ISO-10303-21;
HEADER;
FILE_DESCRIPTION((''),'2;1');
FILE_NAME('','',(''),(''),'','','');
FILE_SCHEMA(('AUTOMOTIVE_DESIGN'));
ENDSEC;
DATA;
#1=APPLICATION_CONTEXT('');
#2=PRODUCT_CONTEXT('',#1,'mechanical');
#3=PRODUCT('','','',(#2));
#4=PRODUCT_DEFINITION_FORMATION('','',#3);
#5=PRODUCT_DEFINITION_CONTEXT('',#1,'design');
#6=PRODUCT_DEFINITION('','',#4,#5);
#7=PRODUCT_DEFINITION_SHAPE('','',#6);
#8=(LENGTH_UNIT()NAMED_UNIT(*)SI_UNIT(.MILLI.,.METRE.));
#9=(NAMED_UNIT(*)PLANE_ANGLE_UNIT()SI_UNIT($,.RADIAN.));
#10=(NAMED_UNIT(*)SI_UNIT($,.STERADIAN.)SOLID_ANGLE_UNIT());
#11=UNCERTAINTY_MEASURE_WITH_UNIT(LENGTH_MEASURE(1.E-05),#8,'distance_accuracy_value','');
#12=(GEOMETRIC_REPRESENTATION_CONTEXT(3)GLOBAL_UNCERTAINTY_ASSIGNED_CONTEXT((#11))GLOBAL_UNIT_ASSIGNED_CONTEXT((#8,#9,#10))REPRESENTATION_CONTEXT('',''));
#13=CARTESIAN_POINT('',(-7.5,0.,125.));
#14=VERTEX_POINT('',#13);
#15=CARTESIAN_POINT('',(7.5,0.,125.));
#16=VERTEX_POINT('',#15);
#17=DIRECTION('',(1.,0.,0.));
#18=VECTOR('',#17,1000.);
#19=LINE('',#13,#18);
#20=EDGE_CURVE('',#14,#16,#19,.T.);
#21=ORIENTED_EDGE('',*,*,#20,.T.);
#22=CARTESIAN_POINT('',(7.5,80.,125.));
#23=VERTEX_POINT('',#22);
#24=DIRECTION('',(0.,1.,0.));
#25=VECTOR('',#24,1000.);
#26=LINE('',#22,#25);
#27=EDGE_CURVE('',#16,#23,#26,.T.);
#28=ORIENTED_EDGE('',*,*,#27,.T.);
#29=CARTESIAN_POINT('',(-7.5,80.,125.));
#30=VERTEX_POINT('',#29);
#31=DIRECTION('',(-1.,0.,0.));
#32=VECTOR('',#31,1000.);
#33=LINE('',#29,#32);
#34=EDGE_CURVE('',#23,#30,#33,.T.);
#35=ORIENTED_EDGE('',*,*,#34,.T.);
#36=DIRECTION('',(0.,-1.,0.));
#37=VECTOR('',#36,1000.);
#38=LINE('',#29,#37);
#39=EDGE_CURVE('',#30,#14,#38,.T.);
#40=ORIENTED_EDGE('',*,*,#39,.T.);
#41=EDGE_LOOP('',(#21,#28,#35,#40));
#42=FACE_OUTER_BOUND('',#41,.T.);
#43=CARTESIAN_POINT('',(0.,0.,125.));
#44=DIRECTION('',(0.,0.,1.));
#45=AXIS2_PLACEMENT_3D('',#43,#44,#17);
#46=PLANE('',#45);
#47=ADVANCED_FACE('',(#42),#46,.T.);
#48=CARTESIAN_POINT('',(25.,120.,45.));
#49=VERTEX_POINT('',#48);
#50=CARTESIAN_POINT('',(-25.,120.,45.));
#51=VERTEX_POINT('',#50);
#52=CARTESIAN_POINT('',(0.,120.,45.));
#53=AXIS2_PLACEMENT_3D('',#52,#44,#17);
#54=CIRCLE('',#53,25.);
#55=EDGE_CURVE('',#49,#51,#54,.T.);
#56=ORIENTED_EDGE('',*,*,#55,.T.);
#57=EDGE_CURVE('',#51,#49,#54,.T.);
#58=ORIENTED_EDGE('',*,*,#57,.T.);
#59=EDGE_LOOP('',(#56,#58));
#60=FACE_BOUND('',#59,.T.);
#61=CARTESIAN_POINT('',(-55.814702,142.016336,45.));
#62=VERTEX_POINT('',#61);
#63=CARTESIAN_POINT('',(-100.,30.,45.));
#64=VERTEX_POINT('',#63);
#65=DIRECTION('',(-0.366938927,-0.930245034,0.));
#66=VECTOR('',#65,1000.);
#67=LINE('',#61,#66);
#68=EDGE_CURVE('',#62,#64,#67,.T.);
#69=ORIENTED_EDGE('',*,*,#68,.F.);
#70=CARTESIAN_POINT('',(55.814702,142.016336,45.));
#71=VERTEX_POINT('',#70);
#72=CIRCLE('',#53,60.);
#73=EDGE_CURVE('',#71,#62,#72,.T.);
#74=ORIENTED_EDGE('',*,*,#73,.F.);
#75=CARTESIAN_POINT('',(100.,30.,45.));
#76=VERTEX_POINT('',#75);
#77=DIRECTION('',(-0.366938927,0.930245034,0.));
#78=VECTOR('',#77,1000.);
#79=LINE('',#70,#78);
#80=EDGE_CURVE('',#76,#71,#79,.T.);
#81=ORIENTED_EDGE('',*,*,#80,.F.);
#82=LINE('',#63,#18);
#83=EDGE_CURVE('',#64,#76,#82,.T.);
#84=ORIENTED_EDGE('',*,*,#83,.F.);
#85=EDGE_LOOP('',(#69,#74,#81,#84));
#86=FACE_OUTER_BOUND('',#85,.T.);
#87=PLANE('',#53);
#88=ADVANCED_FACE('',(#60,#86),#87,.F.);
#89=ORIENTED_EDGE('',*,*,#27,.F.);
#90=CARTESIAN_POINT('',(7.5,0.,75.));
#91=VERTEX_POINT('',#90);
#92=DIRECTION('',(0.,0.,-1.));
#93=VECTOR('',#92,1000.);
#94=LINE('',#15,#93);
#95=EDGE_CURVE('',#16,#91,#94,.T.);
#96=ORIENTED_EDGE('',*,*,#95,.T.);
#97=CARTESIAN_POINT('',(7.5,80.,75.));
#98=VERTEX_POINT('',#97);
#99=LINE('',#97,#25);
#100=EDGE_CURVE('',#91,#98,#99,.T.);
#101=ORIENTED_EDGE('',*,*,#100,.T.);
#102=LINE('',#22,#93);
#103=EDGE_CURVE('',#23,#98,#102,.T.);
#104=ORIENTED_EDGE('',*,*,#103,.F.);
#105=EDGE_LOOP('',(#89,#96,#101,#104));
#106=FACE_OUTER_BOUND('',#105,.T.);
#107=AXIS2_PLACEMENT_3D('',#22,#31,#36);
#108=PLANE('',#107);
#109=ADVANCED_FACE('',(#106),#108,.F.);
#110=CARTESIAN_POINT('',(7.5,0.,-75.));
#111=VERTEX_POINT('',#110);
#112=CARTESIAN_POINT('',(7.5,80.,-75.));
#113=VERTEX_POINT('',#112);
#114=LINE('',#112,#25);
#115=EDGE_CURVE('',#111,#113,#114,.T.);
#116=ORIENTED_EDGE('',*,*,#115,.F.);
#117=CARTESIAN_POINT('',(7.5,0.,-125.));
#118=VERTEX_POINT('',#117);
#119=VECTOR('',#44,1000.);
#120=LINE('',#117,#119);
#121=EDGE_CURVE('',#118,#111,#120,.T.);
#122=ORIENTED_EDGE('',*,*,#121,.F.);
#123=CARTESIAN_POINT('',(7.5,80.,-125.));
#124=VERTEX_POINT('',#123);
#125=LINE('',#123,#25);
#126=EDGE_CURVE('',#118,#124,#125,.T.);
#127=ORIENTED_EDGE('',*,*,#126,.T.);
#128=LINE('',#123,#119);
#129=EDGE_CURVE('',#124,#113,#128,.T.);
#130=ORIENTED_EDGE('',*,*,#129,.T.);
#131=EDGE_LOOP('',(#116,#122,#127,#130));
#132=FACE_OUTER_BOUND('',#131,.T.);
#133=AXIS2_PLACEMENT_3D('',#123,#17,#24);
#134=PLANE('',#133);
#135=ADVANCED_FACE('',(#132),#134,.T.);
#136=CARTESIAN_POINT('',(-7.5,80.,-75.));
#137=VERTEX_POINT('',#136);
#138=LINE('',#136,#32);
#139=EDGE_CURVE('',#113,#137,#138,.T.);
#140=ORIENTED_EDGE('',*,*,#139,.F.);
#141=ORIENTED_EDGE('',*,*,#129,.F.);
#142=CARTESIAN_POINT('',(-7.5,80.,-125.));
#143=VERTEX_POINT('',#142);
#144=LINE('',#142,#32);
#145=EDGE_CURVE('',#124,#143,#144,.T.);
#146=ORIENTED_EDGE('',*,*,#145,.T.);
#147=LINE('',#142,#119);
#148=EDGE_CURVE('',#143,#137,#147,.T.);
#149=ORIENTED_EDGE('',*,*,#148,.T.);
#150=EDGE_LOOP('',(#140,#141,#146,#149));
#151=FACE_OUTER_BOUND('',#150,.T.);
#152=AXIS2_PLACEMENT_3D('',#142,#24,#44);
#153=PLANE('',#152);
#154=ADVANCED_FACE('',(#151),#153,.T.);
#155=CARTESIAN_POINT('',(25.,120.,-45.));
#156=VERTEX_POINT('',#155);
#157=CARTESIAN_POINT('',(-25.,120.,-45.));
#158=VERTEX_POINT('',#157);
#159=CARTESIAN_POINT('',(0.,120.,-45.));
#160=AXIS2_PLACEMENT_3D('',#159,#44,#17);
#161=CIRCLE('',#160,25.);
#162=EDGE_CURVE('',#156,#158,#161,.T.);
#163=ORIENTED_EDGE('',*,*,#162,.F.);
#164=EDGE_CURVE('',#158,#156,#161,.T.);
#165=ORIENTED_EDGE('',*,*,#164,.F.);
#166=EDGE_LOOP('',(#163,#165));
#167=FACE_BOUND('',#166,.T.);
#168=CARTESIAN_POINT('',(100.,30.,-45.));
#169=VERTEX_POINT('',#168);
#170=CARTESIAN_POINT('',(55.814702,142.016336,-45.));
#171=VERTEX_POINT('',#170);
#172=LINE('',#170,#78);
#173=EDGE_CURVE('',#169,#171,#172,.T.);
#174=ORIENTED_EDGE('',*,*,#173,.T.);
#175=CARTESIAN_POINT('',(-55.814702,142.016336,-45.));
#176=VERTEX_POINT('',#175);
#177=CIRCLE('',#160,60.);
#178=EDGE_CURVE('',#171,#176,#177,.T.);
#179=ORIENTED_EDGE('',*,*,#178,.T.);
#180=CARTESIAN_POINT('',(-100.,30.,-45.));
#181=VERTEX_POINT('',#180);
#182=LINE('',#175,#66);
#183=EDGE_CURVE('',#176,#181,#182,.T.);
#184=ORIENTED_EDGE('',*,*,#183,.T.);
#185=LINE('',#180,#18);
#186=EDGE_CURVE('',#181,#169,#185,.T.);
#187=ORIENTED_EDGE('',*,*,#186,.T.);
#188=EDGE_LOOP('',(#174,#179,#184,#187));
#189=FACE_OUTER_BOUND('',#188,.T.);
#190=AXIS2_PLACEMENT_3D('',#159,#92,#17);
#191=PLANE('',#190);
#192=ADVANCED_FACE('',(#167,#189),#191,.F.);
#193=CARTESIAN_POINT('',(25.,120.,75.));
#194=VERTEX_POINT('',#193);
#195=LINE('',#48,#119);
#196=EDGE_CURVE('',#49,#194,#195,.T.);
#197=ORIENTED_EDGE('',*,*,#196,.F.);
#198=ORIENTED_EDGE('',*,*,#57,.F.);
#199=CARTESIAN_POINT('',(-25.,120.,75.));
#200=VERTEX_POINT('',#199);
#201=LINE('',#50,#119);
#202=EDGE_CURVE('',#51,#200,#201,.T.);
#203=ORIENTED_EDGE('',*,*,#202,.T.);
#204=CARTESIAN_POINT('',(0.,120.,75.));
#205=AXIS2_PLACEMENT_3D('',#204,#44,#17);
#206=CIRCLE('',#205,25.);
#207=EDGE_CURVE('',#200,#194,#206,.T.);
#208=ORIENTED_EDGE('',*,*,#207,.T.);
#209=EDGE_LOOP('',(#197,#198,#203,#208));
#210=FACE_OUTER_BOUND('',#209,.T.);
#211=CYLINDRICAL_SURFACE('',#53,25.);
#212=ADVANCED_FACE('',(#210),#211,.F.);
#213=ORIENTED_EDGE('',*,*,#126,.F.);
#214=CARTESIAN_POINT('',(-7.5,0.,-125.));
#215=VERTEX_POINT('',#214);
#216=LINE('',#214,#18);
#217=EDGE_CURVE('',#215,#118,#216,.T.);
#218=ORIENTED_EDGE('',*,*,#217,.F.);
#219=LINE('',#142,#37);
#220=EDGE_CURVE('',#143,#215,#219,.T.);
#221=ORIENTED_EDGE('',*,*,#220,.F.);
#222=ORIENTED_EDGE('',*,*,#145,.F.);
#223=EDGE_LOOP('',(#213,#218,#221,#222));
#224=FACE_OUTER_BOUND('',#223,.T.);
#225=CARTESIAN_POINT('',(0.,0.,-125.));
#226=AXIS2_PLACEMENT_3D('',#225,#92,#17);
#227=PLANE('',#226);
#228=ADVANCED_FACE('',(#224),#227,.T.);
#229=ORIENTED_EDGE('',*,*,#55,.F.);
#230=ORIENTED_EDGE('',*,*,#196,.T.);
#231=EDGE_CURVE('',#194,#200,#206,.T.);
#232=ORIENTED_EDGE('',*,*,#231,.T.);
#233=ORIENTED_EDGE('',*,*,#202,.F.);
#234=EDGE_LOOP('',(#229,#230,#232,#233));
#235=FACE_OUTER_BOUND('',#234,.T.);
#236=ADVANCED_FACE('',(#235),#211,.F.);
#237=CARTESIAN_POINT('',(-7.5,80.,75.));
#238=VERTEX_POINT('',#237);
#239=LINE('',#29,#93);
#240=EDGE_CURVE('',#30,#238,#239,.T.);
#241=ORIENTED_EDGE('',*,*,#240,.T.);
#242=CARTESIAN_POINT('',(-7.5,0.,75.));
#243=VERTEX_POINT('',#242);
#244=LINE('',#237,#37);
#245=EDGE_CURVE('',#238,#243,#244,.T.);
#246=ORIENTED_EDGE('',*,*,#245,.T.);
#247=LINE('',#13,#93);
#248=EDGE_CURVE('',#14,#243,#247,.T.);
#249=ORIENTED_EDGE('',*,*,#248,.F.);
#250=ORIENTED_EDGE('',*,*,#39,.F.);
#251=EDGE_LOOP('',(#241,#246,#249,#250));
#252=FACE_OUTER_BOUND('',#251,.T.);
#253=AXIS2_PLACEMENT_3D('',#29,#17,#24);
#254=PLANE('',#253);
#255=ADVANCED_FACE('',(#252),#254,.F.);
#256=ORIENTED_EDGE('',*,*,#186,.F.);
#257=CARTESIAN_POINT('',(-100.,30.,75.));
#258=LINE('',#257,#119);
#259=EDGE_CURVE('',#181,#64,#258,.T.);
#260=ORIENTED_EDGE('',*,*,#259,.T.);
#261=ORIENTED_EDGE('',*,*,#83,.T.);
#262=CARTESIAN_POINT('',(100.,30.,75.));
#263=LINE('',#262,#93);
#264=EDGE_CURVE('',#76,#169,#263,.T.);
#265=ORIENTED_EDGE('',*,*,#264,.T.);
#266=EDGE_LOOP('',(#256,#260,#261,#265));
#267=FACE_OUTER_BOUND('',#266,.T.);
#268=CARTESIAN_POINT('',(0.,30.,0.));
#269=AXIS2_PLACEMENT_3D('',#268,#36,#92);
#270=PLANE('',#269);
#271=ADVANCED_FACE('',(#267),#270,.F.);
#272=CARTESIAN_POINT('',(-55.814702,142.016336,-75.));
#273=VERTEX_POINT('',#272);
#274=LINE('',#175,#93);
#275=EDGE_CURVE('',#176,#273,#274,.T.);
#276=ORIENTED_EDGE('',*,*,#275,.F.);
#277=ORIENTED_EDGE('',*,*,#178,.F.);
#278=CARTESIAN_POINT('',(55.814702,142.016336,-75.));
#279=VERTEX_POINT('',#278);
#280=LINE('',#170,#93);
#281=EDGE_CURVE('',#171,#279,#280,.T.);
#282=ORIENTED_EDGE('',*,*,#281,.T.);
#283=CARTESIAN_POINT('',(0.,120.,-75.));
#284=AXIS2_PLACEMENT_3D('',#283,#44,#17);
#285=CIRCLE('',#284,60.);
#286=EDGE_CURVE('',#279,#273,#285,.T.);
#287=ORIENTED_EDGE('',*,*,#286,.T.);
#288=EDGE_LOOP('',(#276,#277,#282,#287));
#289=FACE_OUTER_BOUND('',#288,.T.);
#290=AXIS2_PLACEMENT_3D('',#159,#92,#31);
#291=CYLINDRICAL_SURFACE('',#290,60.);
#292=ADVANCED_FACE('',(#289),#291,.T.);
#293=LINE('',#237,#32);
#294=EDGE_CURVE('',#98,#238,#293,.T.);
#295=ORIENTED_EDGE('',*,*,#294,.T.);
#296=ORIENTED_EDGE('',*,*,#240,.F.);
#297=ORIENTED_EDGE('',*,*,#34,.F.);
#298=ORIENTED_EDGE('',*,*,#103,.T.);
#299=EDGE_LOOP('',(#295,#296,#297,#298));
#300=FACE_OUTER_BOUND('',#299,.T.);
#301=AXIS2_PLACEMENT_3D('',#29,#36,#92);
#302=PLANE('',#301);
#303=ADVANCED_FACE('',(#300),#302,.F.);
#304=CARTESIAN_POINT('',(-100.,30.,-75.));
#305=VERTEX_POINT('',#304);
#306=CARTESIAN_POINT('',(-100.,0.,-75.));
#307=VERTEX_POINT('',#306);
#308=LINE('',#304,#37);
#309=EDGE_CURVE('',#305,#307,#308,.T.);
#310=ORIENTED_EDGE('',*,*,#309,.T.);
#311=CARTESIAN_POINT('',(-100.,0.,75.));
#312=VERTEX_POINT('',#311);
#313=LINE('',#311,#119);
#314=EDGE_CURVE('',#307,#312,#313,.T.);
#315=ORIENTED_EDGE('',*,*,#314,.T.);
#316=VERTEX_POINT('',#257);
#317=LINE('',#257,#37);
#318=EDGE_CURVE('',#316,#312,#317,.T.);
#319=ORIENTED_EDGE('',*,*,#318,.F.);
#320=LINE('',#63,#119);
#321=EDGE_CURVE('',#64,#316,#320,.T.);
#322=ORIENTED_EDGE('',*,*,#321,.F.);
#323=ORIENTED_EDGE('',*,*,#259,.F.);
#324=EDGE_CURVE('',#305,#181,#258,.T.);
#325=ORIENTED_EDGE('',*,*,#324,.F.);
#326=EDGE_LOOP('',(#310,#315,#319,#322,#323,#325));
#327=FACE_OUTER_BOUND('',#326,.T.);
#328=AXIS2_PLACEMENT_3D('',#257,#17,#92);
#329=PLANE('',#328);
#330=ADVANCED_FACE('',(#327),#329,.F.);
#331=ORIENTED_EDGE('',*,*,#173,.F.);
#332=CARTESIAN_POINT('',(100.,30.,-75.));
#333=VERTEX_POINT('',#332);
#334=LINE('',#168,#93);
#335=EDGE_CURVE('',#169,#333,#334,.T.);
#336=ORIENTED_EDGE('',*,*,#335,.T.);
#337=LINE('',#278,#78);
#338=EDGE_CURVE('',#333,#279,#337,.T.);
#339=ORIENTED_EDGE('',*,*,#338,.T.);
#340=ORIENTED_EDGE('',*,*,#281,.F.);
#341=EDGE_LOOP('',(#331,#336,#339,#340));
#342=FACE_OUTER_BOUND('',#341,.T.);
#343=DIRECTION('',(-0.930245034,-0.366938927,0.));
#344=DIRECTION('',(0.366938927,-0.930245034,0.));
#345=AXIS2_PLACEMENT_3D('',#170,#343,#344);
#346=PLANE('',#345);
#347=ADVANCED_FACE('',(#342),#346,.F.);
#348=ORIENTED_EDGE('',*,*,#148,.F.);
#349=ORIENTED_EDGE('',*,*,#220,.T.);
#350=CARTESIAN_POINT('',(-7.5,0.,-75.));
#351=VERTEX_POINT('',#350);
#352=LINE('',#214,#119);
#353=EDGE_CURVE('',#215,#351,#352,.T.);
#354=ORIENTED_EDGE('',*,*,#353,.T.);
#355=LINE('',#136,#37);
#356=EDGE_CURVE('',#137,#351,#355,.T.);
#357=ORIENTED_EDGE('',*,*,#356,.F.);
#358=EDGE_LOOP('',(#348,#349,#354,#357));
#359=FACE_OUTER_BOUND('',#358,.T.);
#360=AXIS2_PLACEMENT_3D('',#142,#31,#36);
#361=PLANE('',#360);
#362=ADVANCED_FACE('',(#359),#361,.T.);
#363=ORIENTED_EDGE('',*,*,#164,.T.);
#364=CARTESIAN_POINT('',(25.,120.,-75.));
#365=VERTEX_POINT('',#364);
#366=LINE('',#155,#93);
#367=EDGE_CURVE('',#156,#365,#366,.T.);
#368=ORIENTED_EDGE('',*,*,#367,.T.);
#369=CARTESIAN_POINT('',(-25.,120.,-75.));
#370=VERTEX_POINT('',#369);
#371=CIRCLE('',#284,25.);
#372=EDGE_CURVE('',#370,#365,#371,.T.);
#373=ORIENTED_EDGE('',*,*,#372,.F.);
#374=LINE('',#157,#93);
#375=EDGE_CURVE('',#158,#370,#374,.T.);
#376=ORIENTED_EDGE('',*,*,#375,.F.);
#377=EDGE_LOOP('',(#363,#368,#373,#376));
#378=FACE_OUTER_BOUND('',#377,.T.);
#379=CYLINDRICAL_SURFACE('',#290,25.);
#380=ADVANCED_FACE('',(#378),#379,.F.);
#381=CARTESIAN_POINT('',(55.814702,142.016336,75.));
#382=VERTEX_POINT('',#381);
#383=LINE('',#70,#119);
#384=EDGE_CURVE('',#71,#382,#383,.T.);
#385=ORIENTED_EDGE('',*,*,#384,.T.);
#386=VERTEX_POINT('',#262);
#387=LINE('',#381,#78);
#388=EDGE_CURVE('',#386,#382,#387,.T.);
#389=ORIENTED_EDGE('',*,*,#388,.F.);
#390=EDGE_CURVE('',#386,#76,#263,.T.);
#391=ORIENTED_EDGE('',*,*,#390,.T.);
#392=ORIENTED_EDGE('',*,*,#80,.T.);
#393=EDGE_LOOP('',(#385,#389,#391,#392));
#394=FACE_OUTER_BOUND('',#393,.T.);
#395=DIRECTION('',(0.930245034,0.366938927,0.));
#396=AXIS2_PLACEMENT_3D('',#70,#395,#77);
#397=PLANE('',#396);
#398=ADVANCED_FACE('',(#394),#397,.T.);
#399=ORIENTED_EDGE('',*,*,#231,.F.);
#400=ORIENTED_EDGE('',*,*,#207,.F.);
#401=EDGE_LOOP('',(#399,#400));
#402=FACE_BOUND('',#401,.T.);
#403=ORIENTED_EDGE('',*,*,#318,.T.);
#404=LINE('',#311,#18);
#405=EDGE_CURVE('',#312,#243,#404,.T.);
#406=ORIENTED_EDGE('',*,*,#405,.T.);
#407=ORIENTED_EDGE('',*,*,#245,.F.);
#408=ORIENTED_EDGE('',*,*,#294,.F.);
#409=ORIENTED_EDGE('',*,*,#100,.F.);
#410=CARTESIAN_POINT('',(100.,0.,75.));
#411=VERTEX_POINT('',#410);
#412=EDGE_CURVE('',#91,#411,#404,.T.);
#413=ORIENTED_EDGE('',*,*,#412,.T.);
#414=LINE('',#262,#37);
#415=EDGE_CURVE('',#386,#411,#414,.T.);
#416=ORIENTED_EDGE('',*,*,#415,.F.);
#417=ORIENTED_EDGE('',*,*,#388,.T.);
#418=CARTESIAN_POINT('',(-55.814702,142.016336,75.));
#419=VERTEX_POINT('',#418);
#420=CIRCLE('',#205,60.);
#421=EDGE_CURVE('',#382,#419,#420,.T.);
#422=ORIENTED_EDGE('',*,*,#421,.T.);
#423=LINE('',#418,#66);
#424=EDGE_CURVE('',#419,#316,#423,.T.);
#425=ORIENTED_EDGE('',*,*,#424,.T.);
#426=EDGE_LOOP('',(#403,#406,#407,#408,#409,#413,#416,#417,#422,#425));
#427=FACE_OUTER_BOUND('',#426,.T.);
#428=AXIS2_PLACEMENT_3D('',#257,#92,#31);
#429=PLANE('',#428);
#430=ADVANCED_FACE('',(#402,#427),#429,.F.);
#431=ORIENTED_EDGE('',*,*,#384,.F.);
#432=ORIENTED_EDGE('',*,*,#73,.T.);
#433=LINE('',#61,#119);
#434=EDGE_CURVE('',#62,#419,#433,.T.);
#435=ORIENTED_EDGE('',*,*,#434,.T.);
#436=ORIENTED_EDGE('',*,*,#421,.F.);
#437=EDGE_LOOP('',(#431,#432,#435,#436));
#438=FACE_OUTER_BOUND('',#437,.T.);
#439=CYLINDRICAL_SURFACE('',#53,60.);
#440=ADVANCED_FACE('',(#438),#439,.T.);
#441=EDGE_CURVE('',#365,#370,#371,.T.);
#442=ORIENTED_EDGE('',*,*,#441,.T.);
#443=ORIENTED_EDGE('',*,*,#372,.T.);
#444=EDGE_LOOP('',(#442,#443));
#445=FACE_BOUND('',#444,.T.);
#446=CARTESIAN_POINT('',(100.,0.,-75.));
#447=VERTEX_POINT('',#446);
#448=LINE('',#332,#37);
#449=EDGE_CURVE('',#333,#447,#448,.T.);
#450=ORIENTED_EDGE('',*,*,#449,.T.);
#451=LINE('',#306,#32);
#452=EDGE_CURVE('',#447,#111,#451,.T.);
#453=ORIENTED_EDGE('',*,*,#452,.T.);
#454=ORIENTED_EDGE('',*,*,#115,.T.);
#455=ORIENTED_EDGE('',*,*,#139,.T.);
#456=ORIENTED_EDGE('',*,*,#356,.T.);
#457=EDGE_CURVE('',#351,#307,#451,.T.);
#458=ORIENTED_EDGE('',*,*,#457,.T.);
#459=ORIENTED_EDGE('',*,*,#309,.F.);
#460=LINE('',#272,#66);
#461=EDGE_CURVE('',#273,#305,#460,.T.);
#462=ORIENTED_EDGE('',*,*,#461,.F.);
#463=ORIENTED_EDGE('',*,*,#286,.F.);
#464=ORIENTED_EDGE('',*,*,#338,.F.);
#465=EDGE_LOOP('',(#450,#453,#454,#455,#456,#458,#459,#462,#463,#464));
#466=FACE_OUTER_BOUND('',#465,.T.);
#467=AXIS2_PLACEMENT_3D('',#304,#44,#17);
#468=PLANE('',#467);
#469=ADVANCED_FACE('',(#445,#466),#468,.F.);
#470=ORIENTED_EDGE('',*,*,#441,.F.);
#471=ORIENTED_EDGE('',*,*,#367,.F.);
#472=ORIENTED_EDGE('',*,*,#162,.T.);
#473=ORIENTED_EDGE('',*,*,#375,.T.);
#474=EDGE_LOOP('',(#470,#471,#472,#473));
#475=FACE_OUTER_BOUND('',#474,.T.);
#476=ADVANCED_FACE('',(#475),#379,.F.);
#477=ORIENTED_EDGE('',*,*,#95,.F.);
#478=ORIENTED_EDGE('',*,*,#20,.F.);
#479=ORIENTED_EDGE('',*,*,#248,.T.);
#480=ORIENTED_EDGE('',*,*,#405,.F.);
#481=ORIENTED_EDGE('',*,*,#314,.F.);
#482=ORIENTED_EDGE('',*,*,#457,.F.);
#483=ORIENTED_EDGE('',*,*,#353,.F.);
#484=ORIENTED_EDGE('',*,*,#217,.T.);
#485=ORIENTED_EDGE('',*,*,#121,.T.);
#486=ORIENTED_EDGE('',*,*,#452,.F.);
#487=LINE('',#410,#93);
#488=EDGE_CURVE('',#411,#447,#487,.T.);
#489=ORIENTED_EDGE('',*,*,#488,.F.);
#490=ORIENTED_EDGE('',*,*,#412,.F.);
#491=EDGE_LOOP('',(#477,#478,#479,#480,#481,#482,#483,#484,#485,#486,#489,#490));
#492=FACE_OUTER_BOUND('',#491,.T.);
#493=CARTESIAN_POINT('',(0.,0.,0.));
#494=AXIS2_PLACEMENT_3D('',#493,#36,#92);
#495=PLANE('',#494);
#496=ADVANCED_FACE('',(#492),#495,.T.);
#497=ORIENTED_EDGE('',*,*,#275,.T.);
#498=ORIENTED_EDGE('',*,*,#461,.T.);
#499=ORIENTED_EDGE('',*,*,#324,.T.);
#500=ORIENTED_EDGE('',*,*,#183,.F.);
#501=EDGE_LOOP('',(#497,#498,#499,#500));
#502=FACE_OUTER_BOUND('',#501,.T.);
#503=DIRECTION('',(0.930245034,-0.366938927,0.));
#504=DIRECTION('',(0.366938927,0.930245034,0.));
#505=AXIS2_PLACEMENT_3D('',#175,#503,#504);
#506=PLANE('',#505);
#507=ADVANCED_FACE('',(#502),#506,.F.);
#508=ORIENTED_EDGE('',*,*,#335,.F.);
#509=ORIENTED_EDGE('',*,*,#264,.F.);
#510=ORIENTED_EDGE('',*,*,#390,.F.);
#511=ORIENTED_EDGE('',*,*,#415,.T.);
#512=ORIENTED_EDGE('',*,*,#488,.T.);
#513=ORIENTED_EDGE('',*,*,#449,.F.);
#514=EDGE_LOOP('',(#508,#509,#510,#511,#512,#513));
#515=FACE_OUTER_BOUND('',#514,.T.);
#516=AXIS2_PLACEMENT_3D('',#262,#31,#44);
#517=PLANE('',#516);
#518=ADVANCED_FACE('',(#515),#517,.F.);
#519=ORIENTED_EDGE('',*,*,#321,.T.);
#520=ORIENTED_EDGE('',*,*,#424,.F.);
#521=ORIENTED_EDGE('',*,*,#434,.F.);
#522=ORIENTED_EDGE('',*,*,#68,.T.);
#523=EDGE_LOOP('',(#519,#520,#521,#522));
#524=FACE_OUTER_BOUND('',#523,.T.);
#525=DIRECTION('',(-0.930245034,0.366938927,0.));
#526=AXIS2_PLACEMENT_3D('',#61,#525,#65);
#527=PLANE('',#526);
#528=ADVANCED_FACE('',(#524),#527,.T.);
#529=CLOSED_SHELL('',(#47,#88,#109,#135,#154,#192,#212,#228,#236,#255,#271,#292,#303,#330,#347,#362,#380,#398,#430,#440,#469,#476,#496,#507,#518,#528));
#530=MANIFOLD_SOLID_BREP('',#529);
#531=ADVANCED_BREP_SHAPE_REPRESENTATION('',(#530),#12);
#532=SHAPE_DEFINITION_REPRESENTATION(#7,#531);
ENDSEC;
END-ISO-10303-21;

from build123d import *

# Parameters (mm, degrees)
SKETCH_1_W           = 200
SKETCH_1_H           = 150
BOSS_EXTRUDE_1_DEPTH = 30
SKETCH_2_R           = 25
BOSS_EXTRUDE_2_DEPTH = 30
SKETCH_4_W           = 15
SKETCH_4_H           = 80
BOSS_EXTRUDE_3_DEPTH = 50


with BuildPart() as part:
    # Sketch 1 → Boss-Extrude 1 (new body)
    with BuildSketch(Plane(origin=(0, 0, 0), x_dir=(1, 0, 0), z_dir=(0, 1, 0))):
        Rectangle(SKETCH_1_W, SKETCH_1_H)
    extrude(amount=BOSS_EXTRUDE_1_DEPTH)

    # Sketch 2 → Boss-Extrude 2 (add)
    with BuildSketch(Plane.XY.offset(75)):
        with BuildLine():
            Line((-55.814702058, 142.01633562), (-100, 30))
            Line((-100, 30), (100, 30))
            Line((100, 30), (55.814702058, 142.01633562))
            ThreePointArc((55.814702058, 142.01633562), (0, 180), (-55.814702058, 142.01633562))
        make_face()
        with Locations((0, 120)):
            Circle(SKETCH_2_R, mode=Mode.SUBTRACT)
    boss_extrude_2 = extrude(amount=-BOSS_EXTRUDE_2_DEPTH)

    # Sketch 4 → Boss-Extrude 3 (add)
    with BuildSketch(Plane.XY.offset(75)):
        with Locations((0, 40)):
            Rectangle(SKETCH_4_W, SKETCH_4_H)
    boss_extrude_3 = extrude(amount=BOSS_EXTRUDE_3_DEPTH)

    # Mirror 1: Boss-Extrude 2, Boss-Extrude 3 across plane
    add(boss_extrude_2.mirror(Plane.XY))
    add(boss_extrude_3.mirror(Plane.XY))


solid = part.part
